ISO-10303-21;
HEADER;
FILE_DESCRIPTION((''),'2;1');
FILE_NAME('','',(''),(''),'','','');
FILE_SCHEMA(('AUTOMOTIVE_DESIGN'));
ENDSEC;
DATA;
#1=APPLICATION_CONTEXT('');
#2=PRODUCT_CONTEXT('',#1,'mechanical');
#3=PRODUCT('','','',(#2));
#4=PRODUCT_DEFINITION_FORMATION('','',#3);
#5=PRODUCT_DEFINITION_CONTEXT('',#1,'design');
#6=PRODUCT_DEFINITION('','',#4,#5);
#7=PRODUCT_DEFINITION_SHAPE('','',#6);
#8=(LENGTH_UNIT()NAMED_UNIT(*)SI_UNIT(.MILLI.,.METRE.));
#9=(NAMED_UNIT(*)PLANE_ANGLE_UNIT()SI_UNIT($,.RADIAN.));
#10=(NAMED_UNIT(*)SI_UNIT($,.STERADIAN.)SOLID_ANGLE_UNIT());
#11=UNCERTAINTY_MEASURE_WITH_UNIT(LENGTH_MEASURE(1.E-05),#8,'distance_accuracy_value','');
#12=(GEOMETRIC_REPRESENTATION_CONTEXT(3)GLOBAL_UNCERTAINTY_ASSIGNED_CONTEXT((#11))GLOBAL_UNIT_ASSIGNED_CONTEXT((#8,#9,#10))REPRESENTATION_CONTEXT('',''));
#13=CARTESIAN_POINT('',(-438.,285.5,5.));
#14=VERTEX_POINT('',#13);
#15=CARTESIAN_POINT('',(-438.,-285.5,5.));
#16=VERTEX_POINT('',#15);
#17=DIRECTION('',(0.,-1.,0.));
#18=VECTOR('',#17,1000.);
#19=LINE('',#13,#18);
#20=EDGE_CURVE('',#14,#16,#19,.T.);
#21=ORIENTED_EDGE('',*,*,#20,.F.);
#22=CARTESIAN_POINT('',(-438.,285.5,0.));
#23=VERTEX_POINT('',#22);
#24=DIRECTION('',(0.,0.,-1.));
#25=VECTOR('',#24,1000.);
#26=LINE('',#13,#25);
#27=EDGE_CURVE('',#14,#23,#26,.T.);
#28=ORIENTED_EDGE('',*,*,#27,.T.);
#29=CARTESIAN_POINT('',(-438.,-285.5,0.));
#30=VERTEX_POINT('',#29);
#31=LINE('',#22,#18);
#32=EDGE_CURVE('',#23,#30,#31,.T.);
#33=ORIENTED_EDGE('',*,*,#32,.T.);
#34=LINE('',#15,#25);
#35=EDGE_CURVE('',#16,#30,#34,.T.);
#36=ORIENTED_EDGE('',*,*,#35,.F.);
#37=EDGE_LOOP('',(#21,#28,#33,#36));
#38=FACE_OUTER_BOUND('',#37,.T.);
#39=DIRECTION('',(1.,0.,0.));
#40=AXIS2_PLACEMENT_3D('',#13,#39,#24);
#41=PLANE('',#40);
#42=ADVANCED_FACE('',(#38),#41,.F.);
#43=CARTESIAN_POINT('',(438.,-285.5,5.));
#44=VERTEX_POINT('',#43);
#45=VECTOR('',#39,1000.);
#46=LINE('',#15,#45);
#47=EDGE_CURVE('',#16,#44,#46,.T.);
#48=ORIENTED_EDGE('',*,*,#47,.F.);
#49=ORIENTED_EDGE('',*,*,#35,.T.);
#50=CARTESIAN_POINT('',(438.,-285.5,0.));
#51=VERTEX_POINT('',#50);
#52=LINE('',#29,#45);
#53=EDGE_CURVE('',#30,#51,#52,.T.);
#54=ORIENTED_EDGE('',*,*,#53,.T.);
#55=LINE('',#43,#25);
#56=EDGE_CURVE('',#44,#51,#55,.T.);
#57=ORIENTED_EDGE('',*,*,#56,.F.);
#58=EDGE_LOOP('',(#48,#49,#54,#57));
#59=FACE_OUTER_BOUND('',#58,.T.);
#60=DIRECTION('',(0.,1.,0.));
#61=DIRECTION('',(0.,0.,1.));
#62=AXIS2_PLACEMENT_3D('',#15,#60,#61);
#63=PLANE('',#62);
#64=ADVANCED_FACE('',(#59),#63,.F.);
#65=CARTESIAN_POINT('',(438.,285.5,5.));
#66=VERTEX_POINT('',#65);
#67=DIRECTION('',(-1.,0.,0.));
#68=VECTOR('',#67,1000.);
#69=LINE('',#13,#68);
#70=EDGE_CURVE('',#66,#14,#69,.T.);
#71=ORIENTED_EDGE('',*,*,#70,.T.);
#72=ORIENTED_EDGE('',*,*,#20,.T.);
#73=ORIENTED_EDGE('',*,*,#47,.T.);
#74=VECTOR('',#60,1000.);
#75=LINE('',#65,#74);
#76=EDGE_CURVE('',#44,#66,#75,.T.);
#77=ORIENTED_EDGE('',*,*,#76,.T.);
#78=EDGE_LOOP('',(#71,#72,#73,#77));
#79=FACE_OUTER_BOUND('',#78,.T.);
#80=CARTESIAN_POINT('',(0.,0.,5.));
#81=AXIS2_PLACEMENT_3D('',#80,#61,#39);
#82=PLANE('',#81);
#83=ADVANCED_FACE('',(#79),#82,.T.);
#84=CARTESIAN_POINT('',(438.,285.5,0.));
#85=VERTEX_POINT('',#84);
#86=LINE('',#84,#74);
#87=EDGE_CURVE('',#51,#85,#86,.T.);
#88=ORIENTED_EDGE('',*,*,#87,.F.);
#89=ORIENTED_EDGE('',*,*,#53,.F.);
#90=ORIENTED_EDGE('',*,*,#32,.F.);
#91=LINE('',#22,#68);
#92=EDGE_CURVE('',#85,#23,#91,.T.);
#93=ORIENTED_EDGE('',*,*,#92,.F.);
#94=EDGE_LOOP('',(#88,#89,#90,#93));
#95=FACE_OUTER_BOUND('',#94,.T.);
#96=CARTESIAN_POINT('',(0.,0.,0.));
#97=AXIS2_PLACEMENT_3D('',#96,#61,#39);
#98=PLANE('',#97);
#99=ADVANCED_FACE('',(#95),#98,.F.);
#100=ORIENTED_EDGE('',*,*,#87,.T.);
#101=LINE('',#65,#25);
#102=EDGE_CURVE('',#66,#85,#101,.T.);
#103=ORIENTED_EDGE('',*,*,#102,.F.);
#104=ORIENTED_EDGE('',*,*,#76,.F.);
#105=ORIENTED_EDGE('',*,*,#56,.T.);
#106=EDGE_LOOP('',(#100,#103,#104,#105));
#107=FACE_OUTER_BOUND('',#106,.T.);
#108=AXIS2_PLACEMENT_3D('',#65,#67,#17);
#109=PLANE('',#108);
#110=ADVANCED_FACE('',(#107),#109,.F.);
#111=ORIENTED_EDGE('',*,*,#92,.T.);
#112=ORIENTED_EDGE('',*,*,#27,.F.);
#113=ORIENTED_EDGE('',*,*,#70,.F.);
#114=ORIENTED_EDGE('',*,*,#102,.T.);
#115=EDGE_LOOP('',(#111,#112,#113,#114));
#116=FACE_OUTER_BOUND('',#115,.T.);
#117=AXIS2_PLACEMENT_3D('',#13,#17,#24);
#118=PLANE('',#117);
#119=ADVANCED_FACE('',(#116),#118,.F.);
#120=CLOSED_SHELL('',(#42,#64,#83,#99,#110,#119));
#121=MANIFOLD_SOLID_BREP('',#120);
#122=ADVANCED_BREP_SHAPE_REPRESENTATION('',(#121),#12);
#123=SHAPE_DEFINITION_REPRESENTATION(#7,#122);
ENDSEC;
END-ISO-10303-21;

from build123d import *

# Parameters (mm, degrees)
SKETCH_1_W      = 876
SKETCH_1_H      = 571
EXTRUDE_1_DEPTH = 5


with BuildPart() as part:
    # 草图1 → 凸台-拉伸1 (new body)
    with BuildSketch(Plane.XY):
        Rectangle(SKETCH_1_W, SKETCH_1_H)
    extrude(amount=EXTRUDE_1_DEPTH)


solid = part.part
